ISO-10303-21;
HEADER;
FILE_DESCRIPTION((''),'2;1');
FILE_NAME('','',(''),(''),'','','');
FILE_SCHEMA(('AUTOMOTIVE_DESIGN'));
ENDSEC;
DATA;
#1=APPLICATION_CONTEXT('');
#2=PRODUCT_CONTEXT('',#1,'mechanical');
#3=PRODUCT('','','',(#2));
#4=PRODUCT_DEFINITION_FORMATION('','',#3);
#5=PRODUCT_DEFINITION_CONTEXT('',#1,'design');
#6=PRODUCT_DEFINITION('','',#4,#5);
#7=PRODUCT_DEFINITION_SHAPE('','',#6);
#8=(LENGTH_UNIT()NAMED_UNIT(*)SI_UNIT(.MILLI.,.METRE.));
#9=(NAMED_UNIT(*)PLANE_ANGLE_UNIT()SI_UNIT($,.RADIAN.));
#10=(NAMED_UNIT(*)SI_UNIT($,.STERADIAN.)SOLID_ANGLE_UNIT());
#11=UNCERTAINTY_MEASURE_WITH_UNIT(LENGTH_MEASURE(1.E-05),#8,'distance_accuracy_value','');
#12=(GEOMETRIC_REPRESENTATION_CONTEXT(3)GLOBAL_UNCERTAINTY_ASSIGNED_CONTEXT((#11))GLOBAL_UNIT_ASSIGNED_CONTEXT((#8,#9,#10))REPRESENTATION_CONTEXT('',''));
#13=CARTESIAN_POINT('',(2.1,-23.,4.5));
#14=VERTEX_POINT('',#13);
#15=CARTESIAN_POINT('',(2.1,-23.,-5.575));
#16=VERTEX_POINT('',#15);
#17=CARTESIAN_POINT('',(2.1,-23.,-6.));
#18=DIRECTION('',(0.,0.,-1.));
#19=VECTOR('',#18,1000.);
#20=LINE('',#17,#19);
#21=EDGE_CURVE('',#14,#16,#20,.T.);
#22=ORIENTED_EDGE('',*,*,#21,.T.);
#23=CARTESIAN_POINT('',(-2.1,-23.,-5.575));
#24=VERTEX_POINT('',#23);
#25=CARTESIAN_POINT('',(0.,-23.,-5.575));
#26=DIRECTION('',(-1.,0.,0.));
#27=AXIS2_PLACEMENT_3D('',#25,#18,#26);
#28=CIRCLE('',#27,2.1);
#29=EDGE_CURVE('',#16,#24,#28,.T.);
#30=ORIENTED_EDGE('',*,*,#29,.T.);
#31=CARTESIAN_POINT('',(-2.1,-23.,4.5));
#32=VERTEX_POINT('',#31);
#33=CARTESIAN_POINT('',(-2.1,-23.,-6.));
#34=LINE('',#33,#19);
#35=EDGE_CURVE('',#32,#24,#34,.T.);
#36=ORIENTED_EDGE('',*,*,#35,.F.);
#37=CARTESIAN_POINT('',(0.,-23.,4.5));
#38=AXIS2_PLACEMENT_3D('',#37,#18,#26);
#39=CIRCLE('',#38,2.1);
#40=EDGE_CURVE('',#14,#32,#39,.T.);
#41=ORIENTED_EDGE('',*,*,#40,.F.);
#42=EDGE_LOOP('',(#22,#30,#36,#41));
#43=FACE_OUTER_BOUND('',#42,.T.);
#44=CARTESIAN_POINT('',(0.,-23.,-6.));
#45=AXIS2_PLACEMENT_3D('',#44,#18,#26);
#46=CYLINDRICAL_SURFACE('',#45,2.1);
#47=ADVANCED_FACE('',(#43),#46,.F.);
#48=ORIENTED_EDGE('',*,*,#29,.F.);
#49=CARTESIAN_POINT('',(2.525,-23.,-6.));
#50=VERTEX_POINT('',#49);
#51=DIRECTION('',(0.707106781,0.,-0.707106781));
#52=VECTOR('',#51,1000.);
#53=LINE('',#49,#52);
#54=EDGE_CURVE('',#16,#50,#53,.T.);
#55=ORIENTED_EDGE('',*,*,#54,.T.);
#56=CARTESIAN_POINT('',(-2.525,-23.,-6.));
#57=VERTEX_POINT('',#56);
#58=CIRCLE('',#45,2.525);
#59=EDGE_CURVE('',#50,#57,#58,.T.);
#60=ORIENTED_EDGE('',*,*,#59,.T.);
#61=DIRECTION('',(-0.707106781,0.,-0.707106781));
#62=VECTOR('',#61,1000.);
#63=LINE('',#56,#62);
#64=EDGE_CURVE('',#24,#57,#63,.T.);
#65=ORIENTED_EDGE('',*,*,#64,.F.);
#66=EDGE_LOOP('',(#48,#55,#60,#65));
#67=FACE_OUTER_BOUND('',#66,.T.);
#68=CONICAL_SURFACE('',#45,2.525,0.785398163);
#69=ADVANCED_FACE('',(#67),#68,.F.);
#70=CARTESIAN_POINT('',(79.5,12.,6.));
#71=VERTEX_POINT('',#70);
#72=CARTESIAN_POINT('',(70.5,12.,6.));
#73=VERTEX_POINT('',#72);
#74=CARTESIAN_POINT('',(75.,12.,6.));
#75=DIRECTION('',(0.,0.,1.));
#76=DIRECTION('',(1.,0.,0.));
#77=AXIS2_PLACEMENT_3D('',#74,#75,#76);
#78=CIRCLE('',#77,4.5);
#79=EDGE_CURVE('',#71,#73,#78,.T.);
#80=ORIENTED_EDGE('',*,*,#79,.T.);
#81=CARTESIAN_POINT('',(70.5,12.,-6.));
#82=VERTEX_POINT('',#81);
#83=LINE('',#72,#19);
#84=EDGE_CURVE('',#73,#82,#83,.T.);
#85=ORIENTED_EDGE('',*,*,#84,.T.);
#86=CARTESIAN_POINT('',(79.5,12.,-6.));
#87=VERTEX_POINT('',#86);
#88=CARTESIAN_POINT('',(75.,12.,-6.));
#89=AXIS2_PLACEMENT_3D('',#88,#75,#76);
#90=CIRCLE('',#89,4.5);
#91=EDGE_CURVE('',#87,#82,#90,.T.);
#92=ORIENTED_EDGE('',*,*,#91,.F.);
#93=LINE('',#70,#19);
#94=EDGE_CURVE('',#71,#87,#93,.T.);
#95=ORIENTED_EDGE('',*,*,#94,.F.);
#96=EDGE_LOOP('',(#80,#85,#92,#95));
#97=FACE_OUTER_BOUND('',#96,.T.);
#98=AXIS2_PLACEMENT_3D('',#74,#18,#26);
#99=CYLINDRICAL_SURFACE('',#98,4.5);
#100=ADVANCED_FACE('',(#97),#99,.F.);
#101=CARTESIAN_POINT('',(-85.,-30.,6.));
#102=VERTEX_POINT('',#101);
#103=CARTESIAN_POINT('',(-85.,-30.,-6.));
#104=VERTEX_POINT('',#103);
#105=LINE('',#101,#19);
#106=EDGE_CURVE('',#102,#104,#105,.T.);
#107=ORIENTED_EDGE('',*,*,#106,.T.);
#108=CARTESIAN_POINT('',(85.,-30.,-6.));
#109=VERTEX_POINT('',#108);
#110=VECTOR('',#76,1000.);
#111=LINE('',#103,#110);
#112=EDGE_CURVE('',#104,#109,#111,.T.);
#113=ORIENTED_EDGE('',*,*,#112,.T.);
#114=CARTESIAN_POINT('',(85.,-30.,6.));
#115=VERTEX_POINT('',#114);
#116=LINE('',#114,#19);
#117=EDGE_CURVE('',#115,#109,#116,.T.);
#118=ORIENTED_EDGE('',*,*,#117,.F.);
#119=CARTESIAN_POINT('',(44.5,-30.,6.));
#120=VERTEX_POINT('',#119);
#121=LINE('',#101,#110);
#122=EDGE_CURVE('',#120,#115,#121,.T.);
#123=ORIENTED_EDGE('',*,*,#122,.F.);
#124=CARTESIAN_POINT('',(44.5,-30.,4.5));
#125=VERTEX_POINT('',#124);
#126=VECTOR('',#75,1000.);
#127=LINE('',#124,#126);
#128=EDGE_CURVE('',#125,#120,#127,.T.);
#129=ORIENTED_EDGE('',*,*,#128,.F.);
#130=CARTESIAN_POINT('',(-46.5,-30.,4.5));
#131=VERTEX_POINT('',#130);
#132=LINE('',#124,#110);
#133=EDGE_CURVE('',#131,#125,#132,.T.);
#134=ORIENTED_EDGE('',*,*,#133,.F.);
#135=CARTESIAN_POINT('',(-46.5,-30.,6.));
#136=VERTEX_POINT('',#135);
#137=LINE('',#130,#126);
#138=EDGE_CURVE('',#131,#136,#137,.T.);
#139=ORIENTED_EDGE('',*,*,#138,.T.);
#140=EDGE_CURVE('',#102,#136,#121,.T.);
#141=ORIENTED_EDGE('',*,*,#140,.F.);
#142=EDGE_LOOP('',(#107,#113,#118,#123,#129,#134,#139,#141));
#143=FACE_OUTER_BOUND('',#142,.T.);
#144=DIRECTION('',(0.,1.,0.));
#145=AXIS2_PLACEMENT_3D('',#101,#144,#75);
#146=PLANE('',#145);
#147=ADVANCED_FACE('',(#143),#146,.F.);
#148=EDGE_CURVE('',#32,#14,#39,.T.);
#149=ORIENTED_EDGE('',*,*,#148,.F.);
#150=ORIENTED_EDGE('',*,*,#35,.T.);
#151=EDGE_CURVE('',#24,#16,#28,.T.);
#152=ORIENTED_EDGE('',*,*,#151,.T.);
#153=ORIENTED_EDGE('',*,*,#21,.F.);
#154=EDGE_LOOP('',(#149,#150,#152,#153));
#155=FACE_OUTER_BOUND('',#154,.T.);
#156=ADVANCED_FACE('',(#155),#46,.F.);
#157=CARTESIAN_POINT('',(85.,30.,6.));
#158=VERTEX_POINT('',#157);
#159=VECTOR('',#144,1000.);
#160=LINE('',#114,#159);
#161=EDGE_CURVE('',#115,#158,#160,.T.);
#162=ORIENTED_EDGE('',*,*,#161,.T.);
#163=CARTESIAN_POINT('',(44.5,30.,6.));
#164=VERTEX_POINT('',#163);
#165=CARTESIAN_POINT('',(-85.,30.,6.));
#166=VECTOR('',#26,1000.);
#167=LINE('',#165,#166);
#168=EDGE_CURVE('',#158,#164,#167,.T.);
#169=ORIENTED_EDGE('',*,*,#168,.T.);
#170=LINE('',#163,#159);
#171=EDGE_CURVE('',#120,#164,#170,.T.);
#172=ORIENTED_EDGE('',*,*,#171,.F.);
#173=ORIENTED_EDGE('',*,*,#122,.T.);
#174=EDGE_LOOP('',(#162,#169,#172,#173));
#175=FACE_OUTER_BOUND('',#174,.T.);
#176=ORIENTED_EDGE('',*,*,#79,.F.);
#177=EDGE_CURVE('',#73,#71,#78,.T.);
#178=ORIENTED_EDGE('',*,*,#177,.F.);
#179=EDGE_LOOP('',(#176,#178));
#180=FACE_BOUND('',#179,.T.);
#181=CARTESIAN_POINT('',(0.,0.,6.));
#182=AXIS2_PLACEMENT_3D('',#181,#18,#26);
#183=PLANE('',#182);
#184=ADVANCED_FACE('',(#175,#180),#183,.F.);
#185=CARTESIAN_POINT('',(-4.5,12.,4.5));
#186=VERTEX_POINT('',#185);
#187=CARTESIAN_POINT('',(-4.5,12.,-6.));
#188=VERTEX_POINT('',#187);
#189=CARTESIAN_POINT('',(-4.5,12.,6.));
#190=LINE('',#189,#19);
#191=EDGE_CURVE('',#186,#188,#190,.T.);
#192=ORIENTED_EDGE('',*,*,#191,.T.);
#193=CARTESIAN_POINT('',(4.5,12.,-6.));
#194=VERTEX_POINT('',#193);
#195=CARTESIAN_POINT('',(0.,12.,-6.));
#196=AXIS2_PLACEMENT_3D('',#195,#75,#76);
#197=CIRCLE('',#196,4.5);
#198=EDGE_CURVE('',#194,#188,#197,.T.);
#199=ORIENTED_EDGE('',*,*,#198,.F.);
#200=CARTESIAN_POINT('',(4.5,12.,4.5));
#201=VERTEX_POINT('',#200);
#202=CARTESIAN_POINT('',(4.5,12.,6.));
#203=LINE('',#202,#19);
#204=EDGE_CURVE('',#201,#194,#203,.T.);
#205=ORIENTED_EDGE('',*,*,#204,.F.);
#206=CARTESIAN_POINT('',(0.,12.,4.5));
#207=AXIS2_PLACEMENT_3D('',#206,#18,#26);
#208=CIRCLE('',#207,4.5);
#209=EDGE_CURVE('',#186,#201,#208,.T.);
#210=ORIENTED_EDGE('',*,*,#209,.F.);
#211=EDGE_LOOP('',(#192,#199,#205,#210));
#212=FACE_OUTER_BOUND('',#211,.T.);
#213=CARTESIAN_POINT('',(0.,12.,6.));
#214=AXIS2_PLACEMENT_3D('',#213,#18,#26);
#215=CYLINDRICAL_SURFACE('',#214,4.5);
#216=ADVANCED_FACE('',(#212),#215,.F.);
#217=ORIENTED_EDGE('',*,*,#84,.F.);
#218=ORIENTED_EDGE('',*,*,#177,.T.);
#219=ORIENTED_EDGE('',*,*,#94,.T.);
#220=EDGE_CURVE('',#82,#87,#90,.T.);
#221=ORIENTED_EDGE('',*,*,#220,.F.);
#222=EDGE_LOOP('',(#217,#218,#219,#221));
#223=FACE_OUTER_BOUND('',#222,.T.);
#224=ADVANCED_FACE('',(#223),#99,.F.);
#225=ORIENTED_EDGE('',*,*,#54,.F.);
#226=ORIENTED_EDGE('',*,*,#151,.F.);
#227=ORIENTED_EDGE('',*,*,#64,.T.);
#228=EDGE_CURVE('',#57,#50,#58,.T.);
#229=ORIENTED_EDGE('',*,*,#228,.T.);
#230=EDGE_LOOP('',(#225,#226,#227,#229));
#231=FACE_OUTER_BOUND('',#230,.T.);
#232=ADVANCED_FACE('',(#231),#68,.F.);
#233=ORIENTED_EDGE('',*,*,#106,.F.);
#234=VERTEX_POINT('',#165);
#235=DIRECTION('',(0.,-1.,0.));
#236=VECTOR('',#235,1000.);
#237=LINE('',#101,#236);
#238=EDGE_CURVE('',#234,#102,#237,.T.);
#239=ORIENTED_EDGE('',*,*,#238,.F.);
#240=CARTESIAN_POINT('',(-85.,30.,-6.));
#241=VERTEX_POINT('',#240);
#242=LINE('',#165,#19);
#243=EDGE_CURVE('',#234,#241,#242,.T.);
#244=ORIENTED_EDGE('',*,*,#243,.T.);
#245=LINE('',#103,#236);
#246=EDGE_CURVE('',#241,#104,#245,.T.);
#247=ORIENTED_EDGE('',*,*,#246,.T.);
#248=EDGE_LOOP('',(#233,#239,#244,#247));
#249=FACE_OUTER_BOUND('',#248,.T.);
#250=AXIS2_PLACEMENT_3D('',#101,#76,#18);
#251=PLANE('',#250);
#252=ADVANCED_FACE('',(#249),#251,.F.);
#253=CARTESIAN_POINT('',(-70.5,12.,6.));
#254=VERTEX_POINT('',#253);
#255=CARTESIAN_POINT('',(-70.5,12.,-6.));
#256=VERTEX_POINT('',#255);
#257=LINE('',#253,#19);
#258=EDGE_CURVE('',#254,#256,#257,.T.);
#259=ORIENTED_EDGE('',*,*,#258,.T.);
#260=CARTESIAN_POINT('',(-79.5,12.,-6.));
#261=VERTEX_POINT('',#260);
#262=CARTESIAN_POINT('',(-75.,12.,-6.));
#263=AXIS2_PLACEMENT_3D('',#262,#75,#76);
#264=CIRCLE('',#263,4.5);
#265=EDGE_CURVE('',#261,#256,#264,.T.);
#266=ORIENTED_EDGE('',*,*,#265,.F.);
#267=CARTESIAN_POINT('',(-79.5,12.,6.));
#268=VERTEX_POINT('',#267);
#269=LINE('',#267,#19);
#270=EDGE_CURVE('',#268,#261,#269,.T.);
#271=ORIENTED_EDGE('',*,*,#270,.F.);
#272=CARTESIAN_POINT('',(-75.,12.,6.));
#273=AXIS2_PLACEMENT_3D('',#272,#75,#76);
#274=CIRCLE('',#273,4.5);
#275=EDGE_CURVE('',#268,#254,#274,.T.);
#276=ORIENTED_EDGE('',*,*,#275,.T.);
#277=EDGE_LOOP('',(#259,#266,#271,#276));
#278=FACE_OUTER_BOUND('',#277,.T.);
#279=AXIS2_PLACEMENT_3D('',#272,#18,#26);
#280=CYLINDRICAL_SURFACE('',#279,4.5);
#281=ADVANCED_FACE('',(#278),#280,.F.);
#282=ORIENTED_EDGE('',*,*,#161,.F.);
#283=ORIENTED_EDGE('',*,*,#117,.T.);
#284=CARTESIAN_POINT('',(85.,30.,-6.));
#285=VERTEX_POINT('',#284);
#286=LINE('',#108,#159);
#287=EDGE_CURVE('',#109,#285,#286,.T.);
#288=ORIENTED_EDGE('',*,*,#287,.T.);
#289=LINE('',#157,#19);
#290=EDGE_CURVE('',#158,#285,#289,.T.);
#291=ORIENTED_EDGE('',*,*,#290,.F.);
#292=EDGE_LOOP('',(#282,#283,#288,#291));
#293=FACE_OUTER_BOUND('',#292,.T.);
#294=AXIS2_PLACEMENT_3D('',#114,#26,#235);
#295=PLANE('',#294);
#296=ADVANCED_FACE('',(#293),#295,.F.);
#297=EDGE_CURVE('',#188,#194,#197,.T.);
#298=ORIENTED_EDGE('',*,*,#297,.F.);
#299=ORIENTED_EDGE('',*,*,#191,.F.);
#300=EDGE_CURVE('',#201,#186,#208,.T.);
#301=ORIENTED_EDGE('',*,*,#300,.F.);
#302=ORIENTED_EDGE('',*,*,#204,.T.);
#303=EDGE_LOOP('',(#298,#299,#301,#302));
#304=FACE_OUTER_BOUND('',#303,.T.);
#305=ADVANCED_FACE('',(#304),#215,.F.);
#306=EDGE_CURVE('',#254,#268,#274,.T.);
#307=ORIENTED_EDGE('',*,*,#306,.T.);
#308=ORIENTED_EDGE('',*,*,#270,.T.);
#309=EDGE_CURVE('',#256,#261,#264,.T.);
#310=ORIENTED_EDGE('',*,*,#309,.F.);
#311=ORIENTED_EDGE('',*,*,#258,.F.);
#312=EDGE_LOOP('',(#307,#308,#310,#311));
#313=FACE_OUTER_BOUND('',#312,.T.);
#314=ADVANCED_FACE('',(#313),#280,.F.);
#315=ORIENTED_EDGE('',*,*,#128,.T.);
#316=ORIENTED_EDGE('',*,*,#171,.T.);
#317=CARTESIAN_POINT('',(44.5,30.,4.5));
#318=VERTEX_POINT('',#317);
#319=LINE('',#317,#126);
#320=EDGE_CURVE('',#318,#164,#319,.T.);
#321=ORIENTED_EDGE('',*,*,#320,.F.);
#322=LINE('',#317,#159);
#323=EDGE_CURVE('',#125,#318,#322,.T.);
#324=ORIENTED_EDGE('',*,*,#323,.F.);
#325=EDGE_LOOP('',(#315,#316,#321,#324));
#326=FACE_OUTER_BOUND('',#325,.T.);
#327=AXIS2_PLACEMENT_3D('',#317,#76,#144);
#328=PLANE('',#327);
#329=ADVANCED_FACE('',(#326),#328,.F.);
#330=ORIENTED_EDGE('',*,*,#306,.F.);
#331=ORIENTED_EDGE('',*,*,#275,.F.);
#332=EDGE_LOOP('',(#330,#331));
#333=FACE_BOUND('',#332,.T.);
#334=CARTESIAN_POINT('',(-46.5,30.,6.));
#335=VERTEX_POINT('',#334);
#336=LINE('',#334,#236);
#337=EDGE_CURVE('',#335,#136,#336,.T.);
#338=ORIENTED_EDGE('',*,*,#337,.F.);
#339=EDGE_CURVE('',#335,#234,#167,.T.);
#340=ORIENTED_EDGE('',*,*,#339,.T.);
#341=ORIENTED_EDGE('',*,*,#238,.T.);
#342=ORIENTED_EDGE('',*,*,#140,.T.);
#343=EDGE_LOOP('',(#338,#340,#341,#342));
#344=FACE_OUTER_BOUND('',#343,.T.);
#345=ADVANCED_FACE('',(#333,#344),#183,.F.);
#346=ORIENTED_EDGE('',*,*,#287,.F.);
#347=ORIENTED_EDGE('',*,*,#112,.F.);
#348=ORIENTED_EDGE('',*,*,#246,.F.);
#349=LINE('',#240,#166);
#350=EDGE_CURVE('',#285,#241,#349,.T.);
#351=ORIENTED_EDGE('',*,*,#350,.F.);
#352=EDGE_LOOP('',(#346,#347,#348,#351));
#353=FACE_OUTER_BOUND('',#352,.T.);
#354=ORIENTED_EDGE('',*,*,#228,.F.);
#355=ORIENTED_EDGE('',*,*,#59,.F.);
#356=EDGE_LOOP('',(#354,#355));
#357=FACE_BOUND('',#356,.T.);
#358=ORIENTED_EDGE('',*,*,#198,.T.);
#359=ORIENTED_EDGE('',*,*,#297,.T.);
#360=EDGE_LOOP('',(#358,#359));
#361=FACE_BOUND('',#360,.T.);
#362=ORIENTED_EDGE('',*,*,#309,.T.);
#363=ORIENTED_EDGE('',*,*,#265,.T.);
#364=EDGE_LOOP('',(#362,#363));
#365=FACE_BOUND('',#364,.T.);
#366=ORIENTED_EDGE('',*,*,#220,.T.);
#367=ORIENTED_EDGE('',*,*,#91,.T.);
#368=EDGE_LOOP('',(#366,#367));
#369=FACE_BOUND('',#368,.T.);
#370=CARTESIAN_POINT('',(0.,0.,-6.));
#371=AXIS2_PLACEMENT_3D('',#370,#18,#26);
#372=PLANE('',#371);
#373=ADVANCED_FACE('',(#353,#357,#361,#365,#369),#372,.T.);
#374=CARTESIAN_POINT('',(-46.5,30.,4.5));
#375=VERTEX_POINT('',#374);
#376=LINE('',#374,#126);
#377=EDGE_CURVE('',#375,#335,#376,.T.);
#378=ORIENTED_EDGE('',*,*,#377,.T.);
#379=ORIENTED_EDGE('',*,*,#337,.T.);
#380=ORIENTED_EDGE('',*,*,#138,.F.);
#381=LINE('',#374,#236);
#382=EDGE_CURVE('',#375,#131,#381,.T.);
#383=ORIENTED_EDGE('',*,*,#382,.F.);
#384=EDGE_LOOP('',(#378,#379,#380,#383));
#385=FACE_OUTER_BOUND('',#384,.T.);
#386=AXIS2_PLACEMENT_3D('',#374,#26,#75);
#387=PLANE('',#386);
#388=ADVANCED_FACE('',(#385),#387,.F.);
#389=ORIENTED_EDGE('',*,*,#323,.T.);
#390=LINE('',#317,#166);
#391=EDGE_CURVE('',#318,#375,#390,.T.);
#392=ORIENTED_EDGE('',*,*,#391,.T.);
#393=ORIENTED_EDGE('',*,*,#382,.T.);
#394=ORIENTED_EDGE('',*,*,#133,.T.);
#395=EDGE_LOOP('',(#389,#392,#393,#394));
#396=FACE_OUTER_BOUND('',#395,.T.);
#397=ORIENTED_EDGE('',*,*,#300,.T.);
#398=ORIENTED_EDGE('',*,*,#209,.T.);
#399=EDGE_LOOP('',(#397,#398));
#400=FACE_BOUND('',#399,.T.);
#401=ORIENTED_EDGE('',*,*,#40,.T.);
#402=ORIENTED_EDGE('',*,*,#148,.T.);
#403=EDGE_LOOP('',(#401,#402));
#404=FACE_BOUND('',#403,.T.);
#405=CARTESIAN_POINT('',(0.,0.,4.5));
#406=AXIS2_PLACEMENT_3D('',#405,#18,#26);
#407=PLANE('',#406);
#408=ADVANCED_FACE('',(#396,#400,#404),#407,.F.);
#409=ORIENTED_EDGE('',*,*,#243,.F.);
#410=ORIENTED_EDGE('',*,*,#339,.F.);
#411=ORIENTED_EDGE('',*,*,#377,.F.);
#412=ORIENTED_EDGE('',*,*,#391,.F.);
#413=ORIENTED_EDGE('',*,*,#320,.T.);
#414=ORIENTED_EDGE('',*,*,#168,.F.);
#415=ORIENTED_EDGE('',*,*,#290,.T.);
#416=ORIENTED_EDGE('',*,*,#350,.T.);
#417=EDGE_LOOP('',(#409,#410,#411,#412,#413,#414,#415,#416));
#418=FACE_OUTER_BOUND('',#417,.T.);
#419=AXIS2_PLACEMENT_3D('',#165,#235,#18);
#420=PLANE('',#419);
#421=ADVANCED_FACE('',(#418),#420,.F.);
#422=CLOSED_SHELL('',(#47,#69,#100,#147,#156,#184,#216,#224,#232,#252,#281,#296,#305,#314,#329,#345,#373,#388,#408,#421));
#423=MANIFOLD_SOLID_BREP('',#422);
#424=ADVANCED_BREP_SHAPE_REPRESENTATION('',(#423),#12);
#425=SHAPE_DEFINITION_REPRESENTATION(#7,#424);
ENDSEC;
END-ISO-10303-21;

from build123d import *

# Parameters (mm, degrees)
SKETCH_1_W                   = 170
SKETCH_1_H                   = 60
SKETCH_1_R                   = 4.5
EXTRUDE_1_DEPTH              = 6
SKETCH_2_W                   = 91
SKETCH_2_H                   = 60
CUT_EXTRUDE_1_DEPTH          = 1.5
HOLE_WIZARD_M5_1_D           = 4.2
HOLE_WIZARD_M5_1_CSINK_D     = 5.05
HOLE_WIZARD_M5_1_CSINK_ANGLE = 90


with BuildPart() as part:
    # 草图1 → 凸台-拉伸1 (new, symmetric)
    with BuildSketch(Plane.XY):
        Rectangle(SKETCH_1_W, SKETCH_1_H)
        with Locations((-75, 12)):
            Circle(SKETCH_1_R, mode=Mode.SUBTRACT)
        with Locations((75, 12)):
            Circle(SKETCH_1_R, mode=Mode.SUBTRACT)
        with Locations((0, 12)):
            Circle(SKETCH_1_R, mode=Mode.SUBTRACT)
    extrude(amount=EXTRUDE_1_DEPTH, both=True)

    # 草图2 → 切除-拉伸1 (cut)
    with BuildSketch(Plane.XY.offset(6)):
        with Locations((-1, 0)):
            Rectangle(SKETCH_2_W, SKETCH_2_H)
    extrude(amount=-CUT_EXTRUDE_1_DEPTH, mode=Mode.SUBTRACT)

    # M5 螺纹孔1 (through all)
    with Locations(Plane(origin=(0, -23, -6), x_dir=(-1, 0, 0), z_dir=(0, 0, -1))):
        with Locations((0, 0)):
            CounterSinkHole(HOLE_WIZARD_M5_1_D / 2, HOLE_WIZARD_M5_1_CSINK_D / 2, counter_sink_angle=HOLE_WIZARD_M5_1_CSINK_ANGLE)


solid = part.part
